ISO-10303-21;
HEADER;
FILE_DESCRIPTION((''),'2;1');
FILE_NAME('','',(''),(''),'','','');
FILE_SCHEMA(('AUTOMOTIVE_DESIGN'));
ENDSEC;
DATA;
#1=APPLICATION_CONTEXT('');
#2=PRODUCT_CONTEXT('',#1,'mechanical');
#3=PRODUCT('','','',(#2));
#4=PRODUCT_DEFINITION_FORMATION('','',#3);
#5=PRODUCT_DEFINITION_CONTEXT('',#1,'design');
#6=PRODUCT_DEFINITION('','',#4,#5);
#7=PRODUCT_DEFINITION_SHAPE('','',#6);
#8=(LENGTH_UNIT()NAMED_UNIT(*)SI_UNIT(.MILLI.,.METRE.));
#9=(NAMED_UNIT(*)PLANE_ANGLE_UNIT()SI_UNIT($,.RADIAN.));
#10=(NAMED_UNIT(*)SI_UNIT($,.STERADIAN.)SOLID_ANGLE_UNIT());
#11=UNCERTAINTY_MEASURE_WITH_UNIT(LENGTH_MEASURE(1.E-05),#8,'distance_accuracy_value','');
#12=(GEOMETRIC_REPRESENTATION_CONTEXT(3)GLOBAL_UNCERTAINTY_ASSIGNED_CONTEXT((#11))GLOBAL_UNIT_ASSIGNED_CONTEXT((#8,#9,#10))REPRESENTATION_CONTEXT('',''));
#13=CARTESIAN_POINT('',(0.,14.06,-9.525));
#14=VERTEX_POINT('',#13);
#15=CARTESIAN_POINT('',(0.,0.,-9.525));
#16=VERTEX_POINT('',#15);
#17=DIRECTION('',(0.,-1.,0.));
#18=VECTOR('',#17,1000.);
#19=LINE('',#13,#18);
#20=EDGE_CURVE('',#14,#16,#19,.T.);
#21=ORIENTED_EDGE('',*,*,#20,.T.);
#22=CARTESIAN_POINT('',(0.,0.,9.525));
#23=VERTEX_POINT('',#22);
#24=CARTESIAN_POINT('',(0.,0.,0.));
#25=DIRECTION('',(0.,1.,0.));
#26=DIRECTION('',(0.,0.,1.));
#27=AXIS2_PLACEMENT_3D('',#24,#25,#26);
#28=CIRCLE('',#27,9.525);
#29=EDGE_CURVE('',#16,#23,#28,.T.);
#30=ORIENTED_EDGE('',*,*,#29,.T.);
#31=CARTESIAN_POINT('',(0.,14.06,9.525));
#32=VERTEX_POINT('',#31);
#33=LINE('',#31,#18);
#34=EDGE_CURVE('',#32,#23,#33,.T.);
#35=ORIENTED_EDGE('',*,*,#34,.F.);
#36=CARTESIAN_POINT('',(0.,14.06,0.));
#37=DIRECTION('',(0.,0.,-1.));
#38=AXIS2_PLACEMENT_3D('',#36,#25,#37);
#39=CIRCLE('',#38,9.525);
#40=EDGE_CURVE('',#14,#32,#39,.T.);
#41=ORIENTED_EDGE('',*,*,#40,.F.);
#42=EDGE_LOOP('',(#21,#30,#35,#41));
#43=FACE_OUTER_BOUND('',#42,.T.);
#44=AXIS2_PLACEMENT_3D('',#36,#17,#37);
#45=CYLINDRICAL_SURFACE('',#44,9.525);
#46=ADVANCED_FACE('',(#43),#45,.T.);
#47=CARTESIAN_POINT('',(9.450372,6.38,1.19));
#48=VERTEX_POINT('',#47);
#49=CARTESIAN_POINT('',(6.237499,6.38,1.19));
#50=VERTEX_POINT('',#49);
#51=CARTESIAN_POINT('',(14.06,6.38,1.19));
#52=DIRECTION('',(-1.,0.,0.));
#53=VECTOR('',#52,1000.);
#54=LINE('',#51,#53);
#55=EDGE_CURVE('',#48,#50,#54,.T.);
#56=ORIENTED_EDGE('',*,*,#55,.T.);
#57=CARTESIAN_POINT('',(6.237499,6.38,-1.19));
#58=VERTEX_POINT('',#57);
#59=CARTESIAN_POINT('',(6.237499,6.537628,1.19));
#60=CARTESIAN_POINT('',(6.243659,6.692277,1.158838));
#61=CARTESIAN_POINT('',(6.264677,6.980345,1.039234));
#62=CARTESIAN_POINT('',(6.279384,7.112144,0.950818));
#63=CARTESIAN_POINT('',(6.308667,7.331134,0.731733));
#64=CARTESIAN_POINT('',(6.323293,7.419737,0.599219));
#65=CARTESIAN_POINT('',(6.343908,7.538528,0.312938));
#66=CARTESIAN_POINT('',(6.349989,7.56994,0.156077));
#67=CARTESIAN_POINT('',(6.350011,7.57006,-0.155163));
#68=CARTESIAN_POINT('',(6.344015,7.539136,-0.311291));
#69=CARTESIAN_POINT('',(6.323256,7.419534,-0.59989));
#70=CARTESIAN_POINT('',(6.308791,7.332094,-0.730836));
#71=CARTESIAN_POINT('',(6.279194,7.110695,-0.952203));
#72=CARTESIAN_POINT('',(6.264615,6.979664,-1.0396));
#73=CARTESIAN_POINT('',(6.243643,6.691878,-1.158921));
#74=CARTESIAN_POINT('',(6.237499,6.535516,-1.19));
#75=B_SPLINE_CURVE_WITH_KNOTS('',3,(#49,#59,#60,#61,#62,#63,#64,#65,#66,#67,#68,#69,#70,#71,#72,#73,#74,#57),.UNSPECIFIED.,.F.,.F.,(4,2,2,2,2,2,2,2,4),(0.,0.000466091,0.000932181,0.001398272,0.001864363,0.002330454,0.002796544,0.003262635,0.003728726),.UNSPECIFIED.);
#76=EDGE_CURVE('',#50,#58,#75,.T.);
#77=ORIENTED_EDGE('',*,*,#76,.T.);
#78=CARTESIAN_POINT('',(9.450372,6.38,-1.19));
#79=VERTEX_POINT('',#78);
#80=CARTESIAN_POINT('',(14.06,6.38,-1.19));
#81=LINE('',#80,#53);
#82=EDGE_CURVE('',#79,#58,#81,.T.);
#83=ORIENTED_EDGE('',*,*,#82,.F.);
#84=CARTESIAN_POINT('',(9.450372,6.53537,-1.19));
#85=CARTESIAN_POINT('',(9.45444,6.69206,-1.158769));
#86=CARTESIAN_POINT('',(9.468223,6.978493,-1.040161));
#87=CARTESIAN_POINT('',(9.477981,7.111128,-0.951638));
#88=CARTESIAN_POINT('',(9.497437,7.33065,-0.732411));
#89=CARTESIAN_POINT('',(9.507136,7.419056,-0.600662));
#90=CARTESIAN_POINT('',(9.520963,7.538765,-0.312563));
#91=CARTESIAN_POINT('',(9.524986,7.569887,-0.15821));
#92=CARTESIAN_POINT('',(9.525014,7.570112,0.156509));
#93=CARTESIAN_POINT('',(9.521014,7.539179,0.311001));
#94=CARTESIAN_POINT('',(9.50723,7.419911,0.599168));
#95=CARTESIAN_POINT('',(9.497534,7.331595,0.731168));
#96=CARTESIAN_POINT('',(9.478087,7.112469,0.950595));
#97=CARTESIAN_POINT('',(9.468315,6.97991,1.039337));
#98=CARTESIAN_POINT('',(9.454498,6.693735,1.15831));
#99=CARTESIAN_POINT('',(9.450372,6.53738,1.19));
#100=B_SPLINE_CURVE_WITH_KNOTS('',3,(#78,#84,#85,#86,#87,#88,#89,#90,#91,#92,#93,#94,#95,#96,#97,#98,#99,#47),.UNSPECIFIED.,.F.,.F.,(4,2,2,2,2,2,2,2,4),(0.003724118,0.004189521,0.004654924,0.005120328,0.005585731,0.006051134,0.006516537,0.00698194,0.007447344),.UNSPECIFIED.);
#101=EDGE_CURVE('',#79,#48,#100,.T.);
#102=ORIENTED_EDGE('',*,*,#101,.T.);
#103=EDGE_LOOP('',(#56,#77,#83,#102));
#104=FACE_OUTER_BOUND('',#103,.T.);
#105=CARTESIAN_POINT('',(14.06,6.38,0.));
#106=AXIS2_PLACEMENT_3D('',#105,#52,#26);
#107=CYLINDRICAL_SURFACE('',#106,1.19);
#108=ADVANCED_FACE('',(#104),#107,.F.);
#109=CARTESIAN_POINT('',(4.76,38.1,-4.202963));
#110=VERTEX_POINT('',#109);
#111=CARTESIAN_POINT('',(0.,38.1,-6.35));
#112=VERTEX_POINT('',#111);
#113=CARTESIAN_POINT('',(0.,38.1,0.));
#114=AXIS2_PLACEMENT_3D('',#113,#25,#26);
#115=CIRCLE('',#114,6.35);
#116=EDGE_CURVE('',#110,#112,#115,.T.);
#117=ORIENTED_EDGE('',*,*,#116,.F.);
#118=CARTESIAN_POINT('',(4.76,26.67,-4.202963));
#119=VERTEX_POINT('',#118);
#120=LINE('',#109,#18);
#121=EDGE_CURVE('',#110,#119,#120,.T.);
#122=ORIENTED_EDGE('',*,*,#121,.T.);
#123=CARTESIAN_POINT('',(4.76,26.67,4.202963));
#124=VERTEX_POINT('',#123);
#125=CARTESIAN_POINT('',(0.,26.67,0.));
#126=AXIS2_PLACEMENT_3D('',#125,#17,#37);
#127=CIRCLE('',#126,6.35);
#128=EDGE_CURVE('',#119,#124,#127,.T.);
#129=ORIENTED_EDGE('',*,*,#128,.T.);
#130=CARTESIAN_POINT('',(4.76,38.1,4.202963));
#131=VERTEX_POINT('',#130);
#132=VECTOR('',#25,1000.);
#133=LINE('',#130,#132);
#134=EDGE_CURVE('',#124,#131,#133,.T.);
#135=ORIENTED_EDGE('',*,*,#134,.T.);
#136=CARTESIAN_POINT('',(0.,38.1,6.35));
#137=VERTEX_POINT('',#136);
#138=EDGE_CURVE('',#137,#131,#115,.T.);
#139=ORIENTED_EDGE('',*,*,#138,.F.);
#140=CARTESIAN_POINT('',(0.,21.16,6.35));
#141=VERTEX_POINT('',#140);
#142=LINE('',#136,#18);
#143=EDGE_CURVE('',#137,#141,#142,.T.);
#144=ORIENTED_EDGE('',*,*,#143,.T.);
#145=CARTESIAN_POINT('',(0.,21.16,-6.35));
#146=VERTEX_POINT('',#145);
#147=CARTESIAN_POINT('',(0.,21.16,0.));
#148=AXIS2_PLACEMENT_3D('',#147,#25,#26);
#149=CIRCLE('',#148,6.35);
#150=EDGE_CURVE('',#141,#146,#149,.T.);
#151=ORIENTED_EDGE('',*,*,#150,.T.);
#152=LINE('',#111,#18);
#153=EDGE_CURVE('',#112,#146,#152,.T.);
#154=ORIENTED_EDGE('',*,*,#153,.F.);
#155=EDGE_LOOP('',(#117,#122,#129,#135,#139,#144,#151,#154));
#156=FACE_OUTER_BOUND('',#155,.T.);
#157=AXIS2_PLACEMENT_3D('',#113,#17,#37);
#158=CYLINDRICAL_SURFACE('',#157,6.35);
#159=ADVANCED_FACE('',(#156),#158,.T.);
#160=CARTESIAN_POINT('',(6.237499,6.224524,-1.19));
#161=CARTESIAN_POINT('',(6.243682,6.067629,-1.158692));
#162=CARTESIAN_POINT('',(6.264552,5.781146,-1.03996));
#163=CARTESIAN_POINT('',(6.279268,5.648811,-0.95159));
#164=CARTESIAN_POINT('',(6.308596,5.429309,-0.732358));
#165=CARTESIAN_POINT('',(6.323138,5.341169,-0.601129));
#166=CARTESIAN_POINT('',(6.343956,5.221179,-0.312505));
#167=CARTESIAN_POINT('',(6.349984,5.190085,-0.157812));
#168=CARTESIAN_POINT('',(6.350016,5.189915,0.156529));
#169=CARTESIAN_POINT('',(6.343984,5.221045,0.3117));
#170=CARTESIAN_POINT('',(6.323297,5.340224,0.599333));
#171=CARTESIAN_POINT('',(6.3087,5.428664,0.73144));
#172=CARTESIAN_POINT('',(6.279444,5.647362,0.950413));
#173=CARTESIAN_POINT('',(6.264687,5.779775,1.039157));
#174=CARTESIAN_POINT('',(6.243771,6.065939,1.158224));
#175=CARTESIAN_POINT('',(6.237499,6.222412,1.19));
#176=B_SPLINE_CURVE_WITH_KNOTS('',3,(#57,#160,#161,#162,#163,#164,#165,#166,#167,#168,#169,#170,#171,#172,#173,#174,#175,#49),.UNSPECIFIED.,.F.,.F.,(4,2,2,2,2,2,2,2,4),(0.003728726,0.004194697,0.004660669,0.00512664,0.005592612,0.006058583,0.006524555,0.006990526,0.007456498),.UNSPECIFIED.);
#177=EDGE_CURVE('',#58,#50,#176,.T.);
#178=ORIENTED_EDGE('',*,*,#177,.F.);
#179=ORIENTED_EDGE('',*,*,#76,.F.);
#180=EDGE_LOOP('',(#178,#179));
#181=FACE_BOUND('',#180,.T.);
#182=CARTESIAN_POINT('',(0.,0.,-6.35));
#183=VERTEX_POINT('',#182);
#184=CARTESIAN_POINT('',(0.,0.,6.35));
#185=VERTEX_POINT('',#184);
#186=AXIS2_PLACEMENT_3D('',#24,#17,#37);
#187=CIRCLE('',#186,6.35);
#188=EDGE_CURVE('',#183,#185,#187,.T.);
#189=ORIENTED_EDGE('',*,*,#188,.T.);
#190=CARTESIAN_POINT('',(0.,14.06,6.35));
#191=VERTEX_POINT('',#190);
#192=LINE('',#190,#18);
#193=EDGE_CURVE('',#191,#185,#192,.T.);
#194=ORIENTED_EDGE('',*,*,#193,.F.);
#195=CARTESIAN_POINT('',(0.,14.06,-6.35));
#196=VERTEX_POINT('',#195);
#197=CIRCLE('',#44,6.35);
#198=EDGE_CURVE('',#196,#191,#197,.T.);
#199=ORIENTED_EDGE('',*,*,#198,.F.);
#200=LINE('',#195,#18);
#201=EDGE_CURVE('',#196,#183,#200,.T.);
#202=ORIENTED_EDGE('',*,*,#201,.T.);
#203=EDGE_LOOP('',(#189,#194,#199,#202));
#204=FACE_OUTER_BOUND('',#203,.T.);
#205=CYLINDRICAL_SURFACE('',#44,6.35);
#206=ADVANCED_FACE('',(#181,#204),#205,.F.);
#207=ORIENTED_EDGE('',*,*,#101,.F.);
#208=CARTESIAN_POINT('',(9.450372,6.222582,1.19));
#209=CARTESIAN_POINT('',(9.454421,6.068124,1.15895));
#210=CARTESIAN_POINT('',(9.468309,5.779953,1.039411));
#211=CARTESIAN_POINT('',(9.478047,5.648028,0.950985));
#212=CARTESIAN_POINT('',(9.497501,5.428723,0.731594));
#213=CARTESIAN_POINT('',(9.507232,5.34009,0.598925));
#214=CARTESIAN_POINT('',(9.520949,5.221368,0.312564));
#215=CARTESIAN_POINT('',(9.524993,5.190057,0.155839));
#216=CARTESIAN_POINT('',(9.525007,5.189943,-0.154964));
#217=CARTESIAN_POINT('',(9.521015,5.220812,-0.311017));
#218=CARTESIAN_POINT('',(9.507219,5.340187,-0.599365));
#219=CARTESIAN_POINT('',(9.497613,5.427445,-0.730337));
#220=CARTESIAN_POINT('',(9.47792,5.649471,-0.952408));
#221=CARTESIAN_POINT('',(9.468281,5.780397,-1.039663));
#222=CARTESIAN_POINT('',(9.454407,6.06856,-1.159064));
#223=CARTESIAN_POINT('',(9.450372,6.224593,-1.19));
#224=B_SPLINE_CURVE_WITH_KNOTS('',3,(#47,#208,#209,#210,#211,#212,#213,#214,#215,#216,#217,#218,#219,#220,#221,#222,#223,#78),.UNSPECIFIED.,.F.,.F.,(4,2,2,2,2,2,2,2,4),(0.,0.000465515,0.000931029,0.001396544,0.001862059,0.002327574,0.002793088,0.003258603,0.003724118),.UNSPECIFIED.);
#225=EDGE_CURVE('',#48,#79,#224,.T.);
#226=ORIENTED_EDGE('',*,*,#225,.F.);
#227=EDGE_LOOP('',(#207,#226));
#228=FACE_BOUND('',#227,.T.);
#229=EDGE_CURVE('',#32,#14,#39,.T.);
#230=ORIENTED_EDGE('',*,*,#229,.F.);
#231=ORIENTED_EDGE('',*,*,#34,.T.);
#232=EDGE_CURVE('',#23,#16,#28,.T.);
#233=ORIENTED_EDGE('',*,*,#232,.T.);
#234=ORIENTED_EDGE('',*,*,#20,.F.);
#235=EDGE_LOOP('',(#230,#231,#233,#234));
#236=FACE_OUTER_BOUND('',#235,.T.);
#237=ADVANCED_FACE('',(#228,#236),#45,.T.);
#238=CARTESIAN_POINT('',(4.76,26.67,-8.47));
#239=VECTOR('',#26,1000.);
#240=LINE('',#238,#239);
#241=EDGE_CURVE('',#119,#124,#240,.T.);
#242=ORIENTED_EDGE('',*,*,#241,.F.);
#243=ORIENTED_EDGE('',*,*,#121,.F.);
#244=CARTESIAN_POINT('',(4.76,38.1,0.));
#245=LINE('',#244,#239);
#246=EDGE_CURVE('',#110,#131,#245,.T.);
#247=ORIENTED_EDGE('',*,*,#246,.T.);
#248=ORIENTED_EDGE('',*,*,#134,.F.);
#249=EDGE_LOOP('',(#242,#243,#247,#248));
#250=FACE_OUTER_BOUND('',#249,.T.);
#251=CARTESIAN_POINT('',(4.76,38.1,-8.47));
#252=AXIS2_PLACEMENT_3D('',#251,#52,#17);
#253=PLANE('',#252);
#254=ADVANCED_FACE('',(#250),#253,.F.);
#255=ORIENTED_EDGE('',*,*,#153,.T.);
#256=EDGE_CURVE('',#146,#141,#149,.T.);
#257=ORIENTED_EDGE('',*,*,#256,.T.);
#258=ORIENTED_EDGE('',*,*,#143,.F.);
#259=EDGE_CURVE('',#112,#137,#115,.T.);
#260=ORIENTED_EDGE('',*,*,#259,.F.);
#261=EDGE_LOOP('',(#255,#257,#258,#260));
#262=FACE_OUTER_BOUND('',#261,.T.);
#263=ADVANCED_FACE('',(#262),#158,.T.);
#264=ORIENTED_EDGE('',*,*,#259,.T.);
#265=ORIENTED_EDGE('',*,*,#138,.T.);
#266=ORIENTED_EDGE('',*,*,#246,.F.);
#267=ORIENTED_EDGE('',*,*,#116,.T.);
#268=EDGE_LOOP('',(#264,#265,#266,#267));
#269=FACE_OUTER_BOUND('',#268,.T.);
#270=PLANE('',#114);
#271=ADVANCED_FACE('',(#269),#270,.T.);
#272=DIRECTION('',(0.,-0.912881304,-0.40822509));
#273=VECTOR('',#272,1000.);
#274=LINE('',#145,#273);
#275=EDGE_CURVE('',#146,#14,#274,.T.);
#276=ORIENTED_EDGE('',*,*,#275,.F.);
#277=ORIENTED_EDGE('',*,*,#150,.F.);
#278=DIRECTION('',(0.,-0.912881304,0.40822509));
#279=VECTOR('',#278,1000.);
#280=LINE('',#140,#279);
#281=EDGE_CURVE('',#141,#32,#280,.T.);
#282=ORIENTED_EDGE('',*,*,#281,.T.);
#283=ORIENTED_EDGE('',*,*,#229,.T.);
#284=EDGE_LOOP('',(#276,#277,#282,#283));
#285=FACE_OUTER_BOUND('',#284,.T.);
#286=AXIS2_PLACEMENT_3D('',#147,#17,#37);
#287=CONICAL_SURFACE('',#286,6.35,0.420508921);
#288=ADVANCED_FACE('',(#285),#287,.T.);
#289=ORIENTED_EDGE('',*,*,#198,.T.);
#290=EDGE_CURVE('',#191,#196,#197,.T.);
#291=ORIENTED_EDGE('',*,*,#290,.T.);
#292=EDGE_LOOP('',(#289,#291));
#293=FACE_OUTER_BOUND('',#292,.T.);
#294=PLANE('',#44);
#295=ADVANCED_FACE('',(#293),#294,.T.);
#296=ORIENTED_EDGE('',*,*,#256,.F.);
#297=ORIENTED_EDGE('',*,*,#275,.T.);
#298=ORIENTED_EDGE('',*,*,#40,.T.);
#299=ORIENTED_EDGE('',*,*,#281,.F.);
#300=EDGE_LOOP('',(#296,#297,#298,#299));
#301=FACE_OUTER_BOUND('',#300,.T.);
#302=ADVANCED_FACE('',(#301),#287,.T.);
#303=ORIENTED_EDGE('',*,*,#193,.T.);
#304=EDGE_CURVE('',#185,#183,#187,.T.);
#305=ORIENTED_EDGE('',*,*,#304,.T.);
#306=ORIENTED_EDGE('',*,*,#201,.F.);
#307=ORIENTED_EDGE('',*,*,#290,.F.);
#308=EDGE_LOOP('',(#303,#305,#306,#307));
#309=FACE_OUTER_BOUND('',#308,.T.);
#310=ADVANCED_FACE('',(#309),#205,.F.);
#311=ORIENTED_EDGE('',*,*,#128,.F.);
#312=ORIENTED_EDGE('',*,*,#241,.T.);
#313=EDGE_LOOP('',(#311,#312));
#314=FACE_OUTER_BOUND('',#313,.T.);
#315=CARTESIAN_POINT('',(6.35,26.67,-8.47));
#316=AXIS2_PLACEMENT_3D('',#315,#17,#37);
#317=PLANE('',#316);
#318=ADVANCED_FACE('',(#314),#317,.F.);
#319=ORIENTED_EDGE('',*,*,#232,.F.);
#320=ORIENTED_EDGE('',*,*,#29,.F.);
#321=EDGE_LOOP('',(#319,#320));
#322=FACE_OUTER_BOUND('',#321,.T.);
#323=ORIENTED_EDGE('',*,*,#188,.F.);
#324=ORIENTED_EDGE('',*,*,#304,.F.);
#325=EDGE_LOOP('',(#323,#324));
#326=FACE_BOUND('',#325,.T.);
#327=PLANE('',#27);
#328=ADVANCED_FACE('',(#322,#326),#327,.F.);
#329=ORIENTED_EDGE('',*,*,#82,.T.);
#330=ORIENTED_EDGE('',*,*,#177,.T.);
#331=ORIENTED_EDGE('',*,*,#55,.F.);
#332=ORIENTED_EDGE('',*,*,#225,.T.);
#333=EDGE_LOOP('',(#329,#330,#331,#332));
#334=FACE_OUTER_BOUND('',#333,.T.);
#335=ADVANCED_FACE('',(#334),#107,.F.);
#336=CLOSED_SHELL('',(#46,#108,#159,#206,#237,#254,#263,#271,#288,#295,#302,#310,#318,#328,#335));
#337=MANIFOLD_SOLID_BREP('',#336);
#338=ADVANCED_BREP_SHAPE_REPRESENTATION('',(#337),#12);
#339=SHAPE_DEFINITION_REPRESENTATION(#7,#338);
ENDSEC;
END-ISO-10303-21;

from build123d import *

# Parameters (mm, degrees)
BASE_CYLINDER_SKETCH_19_05_R = 9.525
BASE_CYLINDER_19_05_DEPTH    = 14.06
TAPER_TOP_SKETCH_12_7_R      = 6.35
SHANK_SKETCH_R               = 6.35
SHANK_12_7_DEPTH             = 16.94
SHANK_FLAT_SKETCH_W          = 1.59
SHANK_FLAT_SKETCH_H          = 11.43
SHANK_FLAT_DEPTH             = 8.47
BORE_SKETCH_11_11_R          = 6.35
BORE_11_11_DEPTH             = 14.06
CROSS_HOLE_SKETCH_2_38_R     = 1.19
CROSS_HOLE_2_38_DEPTH        = 14.06


with BuildPart() as part:
    # Base Cylinder Sketch Ø19.05 → Base Cylinder Ø19.05 (new body)
    with BuildSketch(Plane(origin=(0, 0, 0), x_dir=(1, 0, 0), z_dir=(0, 1, 0))):
        with Locations(Location((0, 0, 0), (0, 0, 270))):
            Circle(BASE_CYLINDER_SKETCH_19_05_R)
    extrude(amount=BASE_CYLINDER_19_05_DEPTH)

    # Taper Top Sketch Ø12.7 → section 0 of taper_loft
    with BuildSketch(Plane(origin=(0, 21.16, 0), x_dir=(1, 0, 0), z_dir=(0, 1, 0)), mode=Mode.PRIVATE) as taper_loft_s0:
        Circle(TAPER_TOP_SKETCH_12_7_R)
    # loft up to a face of the part (taper_loft)
    loft([taper_loft_s0.sketch, Face(Wire([part.edges().sort_by_distance((6.943426176, 14.06, -6.520311184))[0]]))])

    # Shank Sketch → Shank Ø12.7 (add)
    with BuildSketch(Plane(origin=(0, 21.16, 0), x_dir=(1, 0, 0), z_dir=(0, 1, 0))):
        with Locations(Location((0, 0, 0), (0, 0, 270))):
            Circle(SHANK_SKETCH_R)
    extrude(amount=SHANK_12_7_DEPTH)

    # Shank Flat Sketch → Shank Flat (cut, symmetric)
    with BuildSketch(Plane.XY):
        with Locations((5.555, 32.385)):
            Rectangle(SHANK_FLAT_SKETCH_W, SHANK_FLAT_SKETCH_H)
    extrude(amount=SHANK_FLAT_DEPTH, both=True, mode=Mode.SUBTRACT)

    # Bore Sketch Ø11.11 → Bore Ø11.11 (cut)
    with BuildSketch(Plane.XZ):
        with Locations(Location((0, 0, 0), (0, 0, 270))):
            Circle(BORE_SKETCH_11_11_R)
    extrude(amount=-BORE_11_11_DEPTH, mode=Mode.SUBTRACT)

    # Cross Hole Sketch Ø2.38 → Cross Hole Ø2.38 (cut)
    with BuildSketch(Plane(origin=(0, 0, 0), x_dir=(0, 0, -1), z_dir=(1, 0, 0))):
        with Locations(Location((0, 6.38, 0), (0, 0, 180))):
            Circle(CROSS_HOLE_SKETCH_2_38_R)
    extrude(amount=CROSS_HOLE_2_38_DEPTH, mode=Mode.SUBTRACT)


solid = part.part
